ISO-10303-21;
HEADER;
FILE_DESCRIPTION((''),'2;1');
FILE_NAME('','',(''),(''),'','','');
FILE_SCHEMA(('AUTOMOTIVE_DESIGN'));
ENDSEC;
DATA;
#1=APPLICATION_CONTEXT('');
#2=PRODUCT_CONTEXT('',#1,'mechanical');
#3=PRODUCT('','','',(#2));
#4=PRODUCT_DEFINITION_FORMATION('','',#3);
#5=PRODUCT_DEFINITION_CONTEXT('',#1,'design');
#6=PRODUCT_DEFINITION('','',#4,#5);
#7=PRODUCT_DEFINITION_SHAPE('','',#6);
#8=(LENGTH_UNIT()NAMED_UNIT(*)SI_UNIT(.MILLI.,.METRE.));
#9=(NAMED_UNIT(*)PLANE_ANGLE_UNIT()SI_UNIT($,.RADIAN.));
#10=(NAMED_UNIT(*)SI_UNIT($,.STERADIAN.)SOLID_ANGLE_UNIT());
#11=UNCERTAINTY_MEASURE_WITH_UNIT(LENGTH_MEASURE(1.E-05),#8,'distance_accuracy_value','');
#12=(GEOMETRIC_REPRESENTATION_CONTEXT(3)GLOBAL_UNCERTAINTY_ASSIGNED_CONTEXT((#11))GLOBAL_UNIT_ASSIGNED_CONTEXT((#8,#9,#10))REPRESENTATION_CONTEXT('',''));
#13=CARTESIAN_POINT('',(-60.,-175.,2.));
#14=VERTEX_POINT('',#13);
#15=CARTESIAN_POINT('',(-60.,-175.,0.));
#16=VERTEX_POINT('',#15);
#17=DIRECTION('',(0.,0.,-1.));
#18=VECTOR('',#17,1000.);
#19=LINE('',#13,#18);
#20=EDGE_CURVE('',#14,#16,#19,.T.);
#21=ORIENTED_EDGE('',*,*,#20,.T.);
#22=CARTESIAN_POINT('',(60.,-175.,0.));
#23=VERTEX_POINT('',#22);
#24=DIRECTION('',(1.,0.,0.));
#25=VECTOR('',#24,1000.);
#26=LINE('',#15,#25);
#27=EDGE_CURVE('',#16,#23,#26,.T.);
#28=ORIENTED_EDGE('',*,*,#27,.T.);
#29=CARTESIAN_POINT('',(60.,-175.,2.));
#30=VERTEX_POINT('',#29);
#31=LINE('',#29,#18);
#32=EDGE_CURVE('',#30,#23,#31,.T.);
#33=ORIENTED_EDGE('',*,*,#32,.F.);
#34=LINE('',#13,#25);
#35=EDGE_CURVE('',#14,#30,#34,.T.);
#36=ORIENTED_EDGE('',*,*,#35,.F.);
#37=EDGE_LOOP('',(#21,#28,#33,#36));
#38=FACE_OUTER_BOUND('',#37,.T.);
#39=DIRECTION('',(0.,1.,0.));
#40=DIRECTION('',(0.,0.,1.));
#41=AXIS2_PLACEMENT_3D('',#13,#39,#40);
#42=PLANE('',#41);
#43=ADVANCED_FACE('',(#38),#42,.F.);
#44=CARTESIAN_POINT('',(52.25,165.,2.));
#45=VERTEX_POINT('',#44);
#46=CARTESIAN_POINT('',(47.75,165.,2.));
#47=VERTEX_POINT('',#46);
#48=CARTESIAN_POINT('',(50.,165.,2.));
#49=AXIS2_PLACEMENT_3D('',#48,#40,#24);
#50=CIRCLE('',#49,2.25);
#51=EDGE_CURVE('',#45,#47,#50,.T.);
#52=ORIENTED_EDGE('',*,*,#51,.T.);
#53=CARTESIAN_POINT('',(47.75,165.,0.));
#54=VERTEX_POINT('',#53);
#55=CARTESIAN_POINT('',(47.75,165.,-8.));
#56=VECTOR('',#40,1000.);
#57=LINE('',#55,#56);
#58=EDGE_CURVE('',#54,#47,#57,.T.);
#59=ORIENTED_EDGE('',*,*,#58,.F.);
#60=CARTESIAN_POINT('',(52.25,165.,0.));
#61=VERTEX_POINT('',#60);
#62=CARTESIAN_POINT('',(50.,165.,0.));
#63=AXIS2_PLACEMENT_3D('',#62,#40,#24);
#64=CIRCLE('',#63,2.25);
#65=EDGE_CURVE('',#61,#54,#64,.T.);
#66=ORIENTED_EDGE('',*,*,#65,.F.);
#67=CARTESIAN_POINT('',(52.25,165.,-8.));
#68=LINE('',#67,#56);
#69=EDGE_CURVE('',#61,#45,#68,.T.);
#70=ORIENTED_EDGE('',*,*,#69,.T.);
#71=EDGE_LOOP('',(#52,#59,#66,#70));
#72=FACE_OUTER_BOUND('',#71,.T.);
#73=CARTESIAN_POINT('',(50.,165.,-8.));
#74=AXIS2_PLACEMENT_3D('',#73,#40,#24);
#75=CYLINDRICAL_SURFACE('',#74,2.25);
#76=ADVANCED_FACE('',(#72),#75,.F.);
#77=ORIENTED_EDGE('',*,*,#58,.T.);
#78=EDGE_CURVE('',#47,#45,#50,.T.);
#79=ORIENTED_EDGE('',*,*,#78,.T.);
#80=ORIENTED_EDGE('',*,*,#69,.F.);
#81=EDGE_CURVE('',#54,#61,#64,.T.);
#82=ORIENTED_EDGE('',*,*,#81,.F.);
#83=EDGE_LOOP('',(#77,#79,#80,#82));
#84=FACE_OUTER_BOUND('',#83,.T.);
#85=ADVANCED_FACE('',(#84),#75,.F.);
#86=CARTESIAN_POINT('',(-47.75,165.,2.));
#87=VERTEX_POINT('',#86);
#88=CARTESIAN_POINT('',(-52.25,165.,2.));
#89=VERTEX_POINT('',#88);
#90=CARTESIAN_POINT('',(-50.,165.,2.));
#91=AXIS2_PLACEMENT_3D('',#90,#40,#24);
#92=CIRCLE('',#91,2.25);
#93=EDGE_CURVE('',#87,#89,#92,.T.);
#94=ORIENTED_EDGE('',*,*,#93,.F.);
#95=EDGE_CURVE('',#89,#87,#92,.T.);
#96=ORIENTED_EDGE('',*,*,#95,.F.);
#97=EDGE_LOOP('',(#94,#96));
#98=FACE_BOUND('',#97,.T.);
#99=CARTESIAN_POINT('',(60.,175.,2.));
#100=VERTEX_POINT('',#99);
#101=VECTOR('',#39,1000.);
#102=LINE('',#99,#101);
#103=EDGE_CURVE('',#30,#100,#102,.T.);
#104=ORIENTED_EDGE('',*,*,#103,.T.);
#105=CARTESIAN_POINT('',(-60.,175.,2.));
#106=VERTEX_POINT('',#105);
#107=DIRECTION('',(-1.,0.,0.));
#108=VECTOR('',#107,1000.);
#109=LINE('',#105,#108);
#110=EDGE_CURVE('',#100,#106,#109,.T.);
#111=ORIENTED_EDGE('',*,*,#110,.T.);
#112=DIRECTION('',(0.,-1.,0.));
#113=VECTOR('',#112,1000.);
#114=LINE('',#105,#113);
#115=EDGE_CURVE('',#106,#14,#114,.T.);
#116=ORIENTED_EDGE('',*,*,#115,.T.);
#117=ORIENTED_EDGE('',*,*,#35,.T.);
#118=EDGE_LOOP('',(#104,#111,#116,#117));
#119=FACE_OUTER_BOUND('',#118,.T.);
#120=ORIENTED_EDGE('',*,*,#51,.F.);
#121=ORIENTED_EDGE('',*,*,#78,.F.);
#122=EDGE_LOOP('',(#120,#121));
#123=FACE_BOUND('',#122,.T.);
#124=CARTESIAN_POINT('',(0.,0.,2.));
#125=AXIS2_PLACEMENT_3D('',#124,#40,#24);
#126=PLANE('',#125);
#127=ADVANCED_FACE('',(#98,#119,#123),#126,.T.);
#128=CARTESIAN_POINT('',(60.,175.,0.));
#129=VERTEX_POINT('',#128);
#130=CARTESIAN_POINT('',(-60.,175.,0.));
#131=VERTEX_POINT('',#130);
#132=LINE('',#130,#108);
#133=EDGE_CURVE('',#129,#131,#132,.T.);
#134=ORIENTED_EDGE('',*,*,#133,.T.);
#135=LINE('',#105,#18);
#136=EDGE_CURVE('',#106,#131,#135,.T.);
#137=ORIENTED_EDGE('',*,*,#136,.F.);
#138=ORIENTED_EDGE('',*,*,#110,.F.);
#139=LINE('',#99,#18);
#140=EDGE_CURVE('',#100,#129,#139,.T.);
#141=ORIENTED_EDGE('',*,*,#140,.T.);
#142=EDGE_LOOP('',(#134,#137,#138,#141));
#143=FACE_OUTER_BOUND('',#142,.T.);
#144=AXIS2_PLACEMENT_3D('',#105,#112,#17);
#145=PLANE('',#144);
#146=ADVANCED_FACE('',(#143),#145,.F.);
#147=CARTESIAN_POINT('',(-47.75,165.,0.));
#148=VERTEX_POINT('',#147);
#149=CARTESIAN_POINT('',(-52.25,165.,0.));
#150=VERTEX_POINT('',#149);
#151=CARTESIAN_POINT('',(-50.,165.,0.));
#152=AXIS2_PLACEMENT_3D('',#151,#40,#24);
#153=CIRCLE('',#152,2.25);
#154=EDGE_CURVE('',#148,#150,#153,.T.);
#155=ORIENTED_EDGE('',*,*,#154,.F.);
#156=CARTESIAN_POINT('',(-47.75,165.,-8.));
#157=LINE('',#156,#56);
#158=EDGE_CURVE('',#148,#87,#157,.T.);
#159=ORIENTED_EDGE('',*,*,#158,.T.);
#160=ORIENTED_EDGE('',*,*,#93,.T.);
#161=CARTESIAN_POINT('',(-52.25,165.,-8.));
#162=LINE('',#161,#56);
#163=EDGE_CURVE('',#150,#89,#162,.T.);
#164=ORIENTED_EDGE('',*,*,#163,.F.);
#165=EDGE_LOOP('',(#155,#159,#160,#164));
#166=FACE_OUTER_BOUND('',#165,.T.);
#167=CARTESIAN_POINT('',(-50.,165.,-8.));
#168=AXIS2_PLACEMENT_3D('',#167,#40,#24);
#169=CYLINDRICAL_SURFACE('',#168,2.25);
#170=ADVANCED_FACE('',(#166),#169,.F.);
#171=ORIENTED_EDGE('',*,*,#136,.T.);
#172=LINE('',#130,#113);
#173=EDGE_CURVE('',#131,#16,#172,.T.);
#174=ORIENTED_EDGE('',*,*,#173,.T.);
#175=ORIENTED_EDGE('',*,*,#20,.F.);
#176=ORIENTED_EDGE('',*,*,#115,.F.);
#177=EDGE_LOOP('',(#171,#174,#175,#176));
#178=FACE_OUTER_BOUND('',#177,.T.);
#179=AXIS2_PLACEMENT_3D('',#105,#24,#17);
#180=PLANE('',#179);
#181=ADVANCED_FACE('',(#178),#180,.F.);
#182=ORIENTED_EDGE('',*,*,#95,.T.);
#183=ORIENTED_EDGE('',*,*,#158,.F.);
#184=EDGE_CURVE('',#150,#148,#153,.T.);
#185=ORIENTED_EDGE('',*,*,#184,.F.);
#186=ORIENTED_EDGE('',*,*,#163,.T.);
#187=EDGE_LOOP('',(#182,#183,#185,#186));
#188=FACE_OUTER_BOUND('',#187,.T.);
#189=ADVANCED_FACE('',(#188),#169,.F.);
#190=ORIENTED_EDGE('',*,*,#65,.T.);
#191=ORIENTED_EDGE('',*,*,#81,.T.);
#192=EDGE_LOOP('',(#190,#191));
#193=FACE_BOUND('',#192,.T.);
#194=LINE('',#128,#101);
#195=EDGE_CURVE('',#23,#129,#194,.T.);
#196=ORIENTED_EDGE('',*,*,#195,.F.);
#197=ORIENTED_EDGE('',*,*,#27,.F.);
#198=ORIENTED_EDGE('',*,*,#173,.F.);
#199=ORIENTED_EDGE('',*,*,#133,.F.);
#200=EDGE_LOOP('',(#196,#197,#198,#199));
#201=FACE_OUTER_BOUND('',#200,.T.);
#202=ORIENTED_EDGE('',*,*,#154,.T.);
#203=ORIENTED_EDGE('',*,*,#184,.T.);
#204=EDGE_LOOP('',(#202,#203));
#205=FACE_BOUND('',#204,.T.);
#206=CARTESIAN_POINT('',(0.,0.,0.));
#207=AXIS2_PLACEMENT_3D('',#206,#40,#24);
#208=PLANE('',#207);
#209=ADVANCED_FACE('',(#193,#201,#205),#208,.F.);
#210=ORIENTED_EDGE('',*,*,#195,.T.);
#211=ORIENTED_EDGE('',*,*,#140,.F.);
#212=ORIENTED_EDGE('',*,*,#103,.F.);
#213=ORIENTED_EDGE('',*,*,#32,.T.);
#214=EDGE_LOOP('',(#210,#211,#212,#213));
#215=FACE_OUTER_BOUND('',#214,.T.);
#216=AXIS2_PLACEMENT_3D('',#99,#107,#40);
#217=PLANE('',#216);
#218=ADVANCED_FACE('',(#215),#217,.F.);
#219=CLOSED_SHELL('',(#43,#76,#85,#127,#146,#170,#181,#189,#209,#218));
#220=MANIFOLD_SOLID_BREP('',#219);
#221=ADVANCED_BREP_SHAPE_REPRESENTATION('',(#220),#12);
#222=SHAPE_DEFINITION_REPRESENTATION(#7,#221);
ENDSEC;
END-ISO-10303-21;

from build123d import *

# Parameters (mm, degrees)
SKETCH_1_W          = 120
SKETCH_1_H          = 350
EXTRUDE_1_DEPTH     = 2
SKETCH_2_R          = 2.25
CUT_EXTRUDE_1_DEPTH = 10


with BuildPart() as part:
    # 草图1 → 凸台-拉伸1 (new body)
    with BuildSketch(Plane.XY):
        Rectangle(SKETCH_1_W, SKETCH_1_H)
    extrude(amount=EXTRUDE_1_DEPTH)

    # 草图2 → 切除-拉伸1 (cut)
    with BuildSketch(Plane.XY.offset(2)):
        with Locations((-50, 165)):
            Circle(SKETCH_2_R)
        with Locations((50, 165)):
            Circle(SKETCH_2_R)
    extrude(amount=-CUT_EXTRUDE_1_DEPTH, mode=Mode.SUBTRACT)


solid = part.part
